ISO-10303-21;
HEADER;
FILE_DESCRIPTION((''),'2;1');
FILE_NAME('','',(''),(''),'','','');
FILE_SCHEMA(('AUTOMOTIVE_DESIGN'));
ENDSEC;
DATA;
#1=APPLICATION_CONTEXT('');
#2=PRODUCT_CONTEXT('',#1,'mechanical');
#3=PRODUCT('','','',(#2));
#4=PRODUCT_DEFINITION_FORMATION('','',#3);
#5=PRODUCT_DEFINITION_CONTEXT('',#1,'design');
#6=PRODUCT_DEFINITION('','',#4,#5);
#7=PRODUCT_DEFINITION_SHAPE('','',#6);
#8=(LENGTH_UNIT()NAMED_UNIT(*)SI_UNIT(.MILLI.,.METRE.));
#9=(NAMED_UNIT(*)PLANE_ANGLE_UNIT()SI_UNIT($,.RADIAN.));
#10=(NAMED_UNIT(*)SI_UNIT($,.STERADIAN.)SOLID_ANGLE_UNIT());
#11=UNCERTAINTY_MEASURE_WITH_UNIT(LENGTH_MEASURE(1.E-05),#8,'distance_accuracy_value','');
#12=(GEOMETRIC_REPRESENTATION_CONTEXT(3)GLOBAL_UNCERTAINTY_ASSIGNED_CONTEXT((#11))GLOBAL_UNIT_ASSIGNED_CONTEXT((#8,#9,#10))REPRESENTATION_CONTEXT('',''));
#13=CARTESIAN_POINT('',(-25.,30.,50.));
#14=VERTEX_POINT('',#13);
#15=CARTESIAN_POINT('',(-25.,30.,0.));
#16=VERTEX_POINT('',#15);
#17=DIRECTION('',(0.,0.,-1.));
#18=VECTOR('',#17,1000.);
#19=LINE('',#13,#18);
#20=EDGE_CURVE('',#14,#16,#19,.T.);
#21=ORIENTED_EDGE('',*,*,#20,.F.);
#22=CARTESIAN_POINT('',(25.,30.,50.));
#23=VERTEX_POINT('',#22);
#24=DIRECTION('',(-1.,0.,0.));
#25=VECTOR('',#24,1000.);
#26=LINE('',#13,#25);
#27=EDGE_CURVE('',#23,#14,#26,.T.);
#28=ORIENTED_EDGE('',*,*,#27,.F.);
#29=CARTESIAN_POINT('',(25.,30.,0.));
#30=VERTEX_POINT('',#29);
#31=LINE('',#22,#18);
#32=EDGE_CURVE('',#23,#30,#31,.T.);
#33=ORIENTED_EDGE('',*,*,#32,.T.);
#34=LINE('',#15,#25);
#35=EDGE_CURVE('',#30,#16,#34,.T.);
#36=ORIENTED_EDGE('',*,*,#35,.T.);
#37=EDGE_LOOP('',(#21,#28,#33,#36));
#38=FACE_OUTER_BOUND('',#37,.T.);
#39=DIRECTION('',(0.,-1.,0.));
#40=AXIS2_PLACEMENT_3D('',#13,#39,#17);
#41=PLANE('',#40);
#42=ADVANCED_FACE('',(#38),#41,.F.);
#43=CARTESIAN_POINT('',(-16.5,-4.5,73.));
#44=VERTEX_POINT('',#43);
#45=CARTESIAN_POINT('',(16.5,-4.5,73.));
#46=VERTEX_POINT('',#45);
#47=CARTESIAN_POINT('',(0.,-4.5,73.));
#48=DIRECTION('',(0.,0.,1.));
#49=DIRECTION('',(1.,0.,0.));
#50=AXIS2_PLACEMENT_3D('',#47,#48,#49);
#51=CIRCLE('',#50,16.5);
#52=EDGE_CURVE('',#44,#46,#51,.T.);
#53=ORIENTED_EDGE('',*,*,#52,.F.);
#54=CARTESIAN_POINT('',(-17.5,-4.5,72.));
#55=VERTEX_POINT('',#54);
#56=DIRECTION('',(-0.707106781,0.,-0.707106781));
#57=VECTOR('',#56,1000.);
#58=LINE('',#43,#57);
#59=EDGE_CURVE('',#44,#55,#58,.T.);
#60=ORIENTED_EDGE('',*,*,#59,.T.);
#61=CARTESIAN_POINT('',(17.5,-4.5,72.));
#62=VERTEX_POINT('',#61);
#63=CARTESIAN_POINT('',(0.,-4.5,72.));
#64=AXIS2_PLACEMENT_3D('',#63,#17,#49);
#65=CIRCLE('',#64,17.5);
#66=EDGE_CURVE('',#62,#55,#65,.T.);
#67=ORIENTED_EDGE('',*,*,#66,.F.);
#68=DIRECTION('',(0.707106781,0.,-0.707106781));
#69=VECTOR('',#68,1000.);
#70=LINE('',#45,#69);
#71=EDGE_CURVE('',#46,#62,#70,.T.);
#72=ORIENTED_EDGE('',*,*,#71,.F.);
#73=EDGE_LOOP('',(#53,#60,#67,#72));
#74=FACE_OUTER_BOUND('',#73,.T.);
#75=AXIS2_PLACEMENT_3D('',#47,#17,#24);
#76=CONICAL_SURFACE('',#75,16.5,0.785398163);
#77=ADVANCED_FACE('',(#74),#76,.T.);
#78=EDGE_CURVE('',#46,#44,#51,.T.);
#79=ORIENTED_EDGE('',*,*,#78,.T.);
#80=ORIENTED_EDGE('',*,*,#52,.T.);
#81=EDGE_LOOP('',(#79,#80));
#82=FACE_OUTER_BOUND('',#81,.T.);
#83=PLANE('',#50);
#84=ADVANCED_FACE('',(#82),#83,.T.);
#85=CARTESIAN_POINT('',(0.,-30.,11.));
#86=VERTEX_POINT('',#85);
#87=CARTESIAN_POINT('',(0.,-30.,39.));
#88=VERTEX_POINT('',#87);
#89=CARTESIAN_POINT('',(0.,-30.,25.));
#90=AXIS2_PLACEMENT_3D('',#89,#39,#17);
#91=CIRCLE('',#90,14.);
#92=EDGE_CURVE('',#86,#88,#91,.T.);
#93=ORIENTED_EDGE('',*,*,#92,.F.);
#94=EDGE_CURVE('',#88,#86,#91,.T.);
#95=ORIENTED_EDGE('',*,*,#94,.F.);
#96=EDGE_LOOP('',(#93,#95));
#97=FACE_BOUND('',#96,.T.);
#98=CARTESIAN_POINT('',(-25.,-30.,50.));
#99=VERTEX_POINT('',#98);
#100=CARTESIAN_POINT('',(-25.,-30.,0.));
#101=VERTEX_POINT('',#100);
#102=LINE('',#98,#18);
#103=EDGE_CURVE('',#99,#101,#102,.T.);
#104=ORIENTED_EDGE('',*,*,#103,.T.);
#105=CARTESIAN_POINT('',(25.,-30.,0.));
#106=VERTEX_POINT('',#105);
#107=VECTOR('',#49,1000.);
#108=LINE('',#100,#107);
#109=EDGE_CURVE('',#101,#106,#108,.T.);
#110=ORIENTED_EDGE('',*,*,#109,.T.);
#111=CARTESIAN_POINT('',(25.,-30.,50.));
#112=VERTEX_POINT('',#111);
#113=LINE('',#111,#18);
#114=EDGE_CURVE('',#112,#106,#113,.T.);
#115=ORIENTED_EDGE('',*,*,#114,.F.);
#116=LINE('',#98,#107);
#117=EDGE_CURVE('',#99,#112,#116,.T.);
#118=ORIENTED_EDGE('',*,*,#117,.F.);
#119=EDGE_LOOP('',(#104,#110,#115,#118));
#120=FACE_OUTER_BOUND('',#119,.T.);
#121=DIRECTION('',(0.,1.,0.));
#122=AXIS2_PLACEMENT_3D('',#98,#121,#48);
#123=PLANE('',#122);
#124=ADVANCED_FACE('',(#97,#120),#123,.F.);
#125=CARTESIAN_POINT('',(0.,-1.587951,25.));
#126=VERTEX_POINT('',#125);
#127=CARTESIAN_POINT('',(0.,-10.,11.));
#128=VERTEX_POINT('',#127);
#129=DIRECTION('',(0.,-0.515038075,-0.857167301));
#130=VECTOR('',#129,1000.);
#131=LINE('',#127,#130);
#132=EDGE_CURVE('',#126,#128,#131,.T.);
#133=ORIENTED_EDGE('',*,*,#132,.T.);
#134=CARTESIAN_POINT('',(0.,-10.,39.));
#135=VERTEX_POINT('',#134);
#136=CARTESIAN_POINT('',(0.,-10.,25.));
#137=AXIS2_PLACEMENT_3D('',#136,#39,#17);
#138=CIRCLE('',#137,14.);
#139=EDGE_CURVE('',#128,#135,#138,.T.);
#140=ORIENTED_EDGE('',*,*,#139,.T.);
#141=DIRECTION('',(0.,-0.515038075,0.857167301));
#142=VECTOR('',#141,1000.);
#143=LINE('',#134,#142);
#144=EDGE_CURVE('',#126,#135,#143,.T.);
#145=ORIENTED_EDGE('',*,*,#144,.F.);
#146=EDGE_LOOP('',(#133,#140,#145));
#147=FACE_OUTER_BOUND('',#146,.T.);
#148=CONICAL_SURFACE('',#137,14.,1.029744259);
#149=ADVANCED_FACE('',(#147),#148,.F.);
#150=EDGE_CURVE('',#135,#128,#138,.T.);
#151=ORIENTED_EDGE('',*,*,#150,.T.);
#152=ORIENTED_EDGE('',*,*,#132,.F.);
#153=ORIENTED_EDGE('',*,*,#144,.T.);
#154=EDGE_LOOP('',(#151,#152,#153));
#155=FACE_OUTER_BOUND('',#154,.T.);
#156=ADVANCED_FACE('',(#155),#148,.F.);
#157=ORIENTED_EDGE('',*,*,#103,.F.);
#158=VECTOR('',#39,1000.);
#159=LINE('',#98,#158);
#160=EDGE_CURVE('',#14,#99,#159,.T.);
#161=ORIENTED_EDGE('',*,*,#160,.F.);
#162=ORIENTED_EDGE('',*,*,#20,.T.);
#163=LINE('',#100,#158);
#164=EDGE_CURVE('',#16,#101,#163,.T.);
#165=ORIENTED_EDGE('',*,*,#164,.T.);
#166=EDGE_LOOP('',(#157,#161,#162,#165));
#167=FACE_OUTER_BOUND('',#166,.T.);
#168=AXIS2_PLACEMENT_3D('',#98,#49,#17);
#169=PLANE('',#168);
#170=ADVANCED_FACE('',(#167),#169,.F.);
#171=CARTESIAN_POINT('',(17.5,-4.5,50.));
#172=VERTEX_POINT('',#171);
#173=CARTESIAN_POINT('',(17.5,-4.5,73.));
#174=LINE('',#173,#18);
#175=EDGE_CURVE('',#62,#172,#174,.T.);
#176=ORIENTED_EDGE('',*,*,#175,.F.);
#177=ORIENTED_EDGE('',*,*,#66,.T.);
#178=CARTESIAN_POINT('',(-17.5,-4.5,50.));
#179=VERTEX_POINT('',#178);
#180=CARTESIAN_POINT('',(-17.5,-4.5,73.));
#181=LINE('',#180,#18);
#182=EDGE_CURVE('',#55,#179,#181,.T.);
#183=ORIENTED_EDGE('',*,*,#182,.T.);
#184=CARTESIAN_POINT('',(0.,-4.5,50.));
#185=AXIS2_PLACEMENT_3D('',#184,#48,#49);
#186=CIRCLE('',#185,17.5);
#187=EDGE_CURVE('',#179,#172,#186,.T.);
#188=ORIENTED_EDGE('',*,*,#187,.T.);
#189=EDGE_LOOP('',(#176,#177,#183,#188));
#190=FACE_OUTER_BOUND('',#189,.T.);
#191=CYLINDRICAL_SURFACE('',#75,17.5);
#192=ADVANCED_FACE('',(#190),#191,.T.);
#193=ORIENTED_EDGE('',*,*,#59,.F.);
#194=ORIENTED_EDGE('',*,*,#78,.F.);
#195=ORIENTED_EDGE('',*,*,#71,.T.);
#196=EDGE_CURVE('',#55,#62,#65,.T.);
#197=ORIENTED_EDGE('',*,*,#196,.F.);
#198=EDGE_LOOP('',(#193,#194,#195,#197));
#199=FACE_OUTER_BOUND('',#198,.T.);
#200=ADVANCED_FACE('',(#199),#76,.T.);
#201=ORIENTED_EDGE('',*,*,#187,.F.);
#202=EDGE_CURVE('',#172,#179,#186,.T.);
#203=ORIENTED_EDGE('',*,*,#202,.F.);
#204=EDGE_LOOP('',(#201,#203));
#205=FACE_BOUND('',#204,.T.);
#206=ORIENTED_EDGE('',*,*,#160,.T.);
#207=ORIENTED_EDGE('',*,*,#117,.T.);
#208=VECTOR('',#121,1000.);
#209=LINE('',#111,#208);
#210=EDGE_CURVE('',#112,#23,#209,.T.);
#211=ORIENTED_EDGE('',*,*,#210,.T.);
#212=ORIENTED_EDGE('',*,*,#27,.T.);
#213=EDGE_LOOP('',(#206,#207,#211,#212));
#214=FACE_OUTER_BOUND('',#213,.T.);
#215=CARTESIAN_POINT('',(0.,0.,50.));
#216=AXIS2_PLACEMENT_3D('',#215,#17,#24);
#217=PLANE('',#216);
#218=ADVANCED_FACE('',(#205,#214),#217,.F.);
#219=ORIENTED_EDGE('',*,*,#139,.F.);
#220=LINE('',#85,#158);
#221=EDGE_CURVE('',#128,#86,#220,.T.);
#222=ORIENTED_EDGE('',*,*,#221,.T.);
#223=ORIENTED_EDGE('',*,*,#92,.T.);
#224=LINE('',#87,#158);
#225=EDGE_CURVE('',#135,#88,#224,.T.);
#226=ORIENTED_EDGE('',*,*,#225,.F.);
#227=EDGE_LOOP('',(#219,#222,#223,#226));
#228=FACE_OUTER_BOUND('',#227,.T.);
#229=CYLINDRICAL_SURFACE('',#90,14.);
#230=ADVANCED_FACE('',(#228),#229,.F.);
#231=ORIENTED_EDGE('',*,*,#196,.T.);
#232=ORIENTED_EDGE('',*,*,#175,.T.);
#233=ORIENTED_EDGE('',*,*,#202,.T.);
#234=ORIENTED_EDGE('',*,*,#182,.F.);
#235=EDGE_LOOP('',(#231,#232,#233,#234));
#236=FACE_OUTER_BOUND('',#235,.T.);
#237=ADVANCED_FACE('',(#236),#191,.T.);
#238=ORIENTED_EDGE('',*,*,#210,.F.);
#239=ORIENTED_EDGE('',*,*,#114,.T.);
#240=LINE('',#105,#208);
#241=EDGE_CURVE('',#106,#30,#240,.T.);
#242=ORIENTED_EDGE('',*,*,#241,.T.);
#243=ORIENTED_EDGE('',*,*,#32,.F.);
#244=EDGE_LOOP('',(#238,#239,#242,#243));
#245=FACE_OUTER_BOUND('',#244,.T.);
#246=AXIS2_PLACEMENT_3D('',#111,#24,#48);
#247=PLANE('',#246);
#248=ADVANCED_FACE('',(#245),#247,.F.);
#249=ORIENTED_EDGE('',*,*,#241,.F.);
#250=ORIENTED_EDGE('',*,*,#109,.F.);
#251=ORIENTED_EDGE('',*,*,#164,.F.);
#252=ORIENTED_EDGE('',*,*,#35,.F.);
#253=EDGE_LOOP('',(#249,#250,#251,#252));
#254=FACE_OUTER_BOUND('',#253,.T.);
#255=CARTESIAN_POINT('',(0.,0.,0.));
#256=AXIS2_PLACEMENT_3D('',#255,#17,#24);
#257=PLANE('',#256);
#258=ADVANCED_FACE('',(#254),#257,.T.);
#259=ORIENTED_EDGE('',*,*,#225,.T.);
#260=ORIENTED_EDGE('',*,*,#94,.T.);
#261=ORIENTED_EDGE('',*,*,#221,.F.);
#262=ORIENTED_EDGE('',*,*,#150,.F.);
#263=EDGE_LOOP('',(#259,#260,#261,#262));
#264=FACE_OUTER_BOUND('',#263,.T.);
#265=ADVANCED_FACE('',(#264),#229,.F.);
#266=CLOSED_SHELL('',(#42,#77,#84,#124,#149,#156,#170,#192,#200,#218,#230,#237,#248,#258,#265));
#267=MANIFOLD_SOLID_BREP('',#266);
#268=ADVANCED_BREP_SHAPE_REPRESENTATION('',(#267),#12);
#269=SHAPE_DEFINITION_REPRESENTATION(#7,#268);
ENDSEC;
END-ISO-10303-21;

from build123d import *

# Parameters (mm, degrees)
SKETCH_1_W      = 50
SKETCH_1_H      = 60
EXTRUDE_1_DEPTH = 50
SKETCH_2_R      = 17.5
EXTRUDE_2_DEPTH = 23
M30X2_0_1_D     = 28
M30X2_0_1_DEPTH = 20
M30X2_0_1_TIP   = 8.412048666
CHAMFER_1_SIZE  = 1


with BuildPart() as part:
    # 草图1 → 凸台-拉伸1 (new body)
    with BuildSketch(Plane.XY):
        Rectangle(SKETCH_1_W, SKETCH_1_H)
    extrude(amount=EXTRUDE_1_DEPTH)

    # 草图2 → 凸台-拉伸2 (add)
    with BuildSketch(Plane.XY.offset(50)):
        with Locations((0, -4.5)):
            Circle(SKETCH_2_R)
    extrude(amount=EXTRUDE_2_DEPTH)

    # M30x2.0 螺纹孔1
    with Locations(Plane(origin=(0, -30, 0), x_dir=(-1, 0, 0), z_dir=(0, -1, 0))):
        with Locations((0, -25)):
            Hole(M30X2_0_1_D / 2, depth=M30X2_0_1_DEPTH)
            with Locations((0, 0, -(M30X2_0_1_DEPTH + M30X2_0_1_TIP / 2))):  # 118° drill point
                Cone(0, M30X2_0_1_D / 2, M30X2_0_1_TIP, mode=Mode.SUBTRACT)

    # 倒角1
    chamfer_1_edges = [part.edges().sort_by_distance(p)[0] for p in [
        (-17.5, -4.5, 73),
    ]]
    chamfer(chamfer_1_edges, length=CHAMFER_1_SIZE)


solid = part.part
